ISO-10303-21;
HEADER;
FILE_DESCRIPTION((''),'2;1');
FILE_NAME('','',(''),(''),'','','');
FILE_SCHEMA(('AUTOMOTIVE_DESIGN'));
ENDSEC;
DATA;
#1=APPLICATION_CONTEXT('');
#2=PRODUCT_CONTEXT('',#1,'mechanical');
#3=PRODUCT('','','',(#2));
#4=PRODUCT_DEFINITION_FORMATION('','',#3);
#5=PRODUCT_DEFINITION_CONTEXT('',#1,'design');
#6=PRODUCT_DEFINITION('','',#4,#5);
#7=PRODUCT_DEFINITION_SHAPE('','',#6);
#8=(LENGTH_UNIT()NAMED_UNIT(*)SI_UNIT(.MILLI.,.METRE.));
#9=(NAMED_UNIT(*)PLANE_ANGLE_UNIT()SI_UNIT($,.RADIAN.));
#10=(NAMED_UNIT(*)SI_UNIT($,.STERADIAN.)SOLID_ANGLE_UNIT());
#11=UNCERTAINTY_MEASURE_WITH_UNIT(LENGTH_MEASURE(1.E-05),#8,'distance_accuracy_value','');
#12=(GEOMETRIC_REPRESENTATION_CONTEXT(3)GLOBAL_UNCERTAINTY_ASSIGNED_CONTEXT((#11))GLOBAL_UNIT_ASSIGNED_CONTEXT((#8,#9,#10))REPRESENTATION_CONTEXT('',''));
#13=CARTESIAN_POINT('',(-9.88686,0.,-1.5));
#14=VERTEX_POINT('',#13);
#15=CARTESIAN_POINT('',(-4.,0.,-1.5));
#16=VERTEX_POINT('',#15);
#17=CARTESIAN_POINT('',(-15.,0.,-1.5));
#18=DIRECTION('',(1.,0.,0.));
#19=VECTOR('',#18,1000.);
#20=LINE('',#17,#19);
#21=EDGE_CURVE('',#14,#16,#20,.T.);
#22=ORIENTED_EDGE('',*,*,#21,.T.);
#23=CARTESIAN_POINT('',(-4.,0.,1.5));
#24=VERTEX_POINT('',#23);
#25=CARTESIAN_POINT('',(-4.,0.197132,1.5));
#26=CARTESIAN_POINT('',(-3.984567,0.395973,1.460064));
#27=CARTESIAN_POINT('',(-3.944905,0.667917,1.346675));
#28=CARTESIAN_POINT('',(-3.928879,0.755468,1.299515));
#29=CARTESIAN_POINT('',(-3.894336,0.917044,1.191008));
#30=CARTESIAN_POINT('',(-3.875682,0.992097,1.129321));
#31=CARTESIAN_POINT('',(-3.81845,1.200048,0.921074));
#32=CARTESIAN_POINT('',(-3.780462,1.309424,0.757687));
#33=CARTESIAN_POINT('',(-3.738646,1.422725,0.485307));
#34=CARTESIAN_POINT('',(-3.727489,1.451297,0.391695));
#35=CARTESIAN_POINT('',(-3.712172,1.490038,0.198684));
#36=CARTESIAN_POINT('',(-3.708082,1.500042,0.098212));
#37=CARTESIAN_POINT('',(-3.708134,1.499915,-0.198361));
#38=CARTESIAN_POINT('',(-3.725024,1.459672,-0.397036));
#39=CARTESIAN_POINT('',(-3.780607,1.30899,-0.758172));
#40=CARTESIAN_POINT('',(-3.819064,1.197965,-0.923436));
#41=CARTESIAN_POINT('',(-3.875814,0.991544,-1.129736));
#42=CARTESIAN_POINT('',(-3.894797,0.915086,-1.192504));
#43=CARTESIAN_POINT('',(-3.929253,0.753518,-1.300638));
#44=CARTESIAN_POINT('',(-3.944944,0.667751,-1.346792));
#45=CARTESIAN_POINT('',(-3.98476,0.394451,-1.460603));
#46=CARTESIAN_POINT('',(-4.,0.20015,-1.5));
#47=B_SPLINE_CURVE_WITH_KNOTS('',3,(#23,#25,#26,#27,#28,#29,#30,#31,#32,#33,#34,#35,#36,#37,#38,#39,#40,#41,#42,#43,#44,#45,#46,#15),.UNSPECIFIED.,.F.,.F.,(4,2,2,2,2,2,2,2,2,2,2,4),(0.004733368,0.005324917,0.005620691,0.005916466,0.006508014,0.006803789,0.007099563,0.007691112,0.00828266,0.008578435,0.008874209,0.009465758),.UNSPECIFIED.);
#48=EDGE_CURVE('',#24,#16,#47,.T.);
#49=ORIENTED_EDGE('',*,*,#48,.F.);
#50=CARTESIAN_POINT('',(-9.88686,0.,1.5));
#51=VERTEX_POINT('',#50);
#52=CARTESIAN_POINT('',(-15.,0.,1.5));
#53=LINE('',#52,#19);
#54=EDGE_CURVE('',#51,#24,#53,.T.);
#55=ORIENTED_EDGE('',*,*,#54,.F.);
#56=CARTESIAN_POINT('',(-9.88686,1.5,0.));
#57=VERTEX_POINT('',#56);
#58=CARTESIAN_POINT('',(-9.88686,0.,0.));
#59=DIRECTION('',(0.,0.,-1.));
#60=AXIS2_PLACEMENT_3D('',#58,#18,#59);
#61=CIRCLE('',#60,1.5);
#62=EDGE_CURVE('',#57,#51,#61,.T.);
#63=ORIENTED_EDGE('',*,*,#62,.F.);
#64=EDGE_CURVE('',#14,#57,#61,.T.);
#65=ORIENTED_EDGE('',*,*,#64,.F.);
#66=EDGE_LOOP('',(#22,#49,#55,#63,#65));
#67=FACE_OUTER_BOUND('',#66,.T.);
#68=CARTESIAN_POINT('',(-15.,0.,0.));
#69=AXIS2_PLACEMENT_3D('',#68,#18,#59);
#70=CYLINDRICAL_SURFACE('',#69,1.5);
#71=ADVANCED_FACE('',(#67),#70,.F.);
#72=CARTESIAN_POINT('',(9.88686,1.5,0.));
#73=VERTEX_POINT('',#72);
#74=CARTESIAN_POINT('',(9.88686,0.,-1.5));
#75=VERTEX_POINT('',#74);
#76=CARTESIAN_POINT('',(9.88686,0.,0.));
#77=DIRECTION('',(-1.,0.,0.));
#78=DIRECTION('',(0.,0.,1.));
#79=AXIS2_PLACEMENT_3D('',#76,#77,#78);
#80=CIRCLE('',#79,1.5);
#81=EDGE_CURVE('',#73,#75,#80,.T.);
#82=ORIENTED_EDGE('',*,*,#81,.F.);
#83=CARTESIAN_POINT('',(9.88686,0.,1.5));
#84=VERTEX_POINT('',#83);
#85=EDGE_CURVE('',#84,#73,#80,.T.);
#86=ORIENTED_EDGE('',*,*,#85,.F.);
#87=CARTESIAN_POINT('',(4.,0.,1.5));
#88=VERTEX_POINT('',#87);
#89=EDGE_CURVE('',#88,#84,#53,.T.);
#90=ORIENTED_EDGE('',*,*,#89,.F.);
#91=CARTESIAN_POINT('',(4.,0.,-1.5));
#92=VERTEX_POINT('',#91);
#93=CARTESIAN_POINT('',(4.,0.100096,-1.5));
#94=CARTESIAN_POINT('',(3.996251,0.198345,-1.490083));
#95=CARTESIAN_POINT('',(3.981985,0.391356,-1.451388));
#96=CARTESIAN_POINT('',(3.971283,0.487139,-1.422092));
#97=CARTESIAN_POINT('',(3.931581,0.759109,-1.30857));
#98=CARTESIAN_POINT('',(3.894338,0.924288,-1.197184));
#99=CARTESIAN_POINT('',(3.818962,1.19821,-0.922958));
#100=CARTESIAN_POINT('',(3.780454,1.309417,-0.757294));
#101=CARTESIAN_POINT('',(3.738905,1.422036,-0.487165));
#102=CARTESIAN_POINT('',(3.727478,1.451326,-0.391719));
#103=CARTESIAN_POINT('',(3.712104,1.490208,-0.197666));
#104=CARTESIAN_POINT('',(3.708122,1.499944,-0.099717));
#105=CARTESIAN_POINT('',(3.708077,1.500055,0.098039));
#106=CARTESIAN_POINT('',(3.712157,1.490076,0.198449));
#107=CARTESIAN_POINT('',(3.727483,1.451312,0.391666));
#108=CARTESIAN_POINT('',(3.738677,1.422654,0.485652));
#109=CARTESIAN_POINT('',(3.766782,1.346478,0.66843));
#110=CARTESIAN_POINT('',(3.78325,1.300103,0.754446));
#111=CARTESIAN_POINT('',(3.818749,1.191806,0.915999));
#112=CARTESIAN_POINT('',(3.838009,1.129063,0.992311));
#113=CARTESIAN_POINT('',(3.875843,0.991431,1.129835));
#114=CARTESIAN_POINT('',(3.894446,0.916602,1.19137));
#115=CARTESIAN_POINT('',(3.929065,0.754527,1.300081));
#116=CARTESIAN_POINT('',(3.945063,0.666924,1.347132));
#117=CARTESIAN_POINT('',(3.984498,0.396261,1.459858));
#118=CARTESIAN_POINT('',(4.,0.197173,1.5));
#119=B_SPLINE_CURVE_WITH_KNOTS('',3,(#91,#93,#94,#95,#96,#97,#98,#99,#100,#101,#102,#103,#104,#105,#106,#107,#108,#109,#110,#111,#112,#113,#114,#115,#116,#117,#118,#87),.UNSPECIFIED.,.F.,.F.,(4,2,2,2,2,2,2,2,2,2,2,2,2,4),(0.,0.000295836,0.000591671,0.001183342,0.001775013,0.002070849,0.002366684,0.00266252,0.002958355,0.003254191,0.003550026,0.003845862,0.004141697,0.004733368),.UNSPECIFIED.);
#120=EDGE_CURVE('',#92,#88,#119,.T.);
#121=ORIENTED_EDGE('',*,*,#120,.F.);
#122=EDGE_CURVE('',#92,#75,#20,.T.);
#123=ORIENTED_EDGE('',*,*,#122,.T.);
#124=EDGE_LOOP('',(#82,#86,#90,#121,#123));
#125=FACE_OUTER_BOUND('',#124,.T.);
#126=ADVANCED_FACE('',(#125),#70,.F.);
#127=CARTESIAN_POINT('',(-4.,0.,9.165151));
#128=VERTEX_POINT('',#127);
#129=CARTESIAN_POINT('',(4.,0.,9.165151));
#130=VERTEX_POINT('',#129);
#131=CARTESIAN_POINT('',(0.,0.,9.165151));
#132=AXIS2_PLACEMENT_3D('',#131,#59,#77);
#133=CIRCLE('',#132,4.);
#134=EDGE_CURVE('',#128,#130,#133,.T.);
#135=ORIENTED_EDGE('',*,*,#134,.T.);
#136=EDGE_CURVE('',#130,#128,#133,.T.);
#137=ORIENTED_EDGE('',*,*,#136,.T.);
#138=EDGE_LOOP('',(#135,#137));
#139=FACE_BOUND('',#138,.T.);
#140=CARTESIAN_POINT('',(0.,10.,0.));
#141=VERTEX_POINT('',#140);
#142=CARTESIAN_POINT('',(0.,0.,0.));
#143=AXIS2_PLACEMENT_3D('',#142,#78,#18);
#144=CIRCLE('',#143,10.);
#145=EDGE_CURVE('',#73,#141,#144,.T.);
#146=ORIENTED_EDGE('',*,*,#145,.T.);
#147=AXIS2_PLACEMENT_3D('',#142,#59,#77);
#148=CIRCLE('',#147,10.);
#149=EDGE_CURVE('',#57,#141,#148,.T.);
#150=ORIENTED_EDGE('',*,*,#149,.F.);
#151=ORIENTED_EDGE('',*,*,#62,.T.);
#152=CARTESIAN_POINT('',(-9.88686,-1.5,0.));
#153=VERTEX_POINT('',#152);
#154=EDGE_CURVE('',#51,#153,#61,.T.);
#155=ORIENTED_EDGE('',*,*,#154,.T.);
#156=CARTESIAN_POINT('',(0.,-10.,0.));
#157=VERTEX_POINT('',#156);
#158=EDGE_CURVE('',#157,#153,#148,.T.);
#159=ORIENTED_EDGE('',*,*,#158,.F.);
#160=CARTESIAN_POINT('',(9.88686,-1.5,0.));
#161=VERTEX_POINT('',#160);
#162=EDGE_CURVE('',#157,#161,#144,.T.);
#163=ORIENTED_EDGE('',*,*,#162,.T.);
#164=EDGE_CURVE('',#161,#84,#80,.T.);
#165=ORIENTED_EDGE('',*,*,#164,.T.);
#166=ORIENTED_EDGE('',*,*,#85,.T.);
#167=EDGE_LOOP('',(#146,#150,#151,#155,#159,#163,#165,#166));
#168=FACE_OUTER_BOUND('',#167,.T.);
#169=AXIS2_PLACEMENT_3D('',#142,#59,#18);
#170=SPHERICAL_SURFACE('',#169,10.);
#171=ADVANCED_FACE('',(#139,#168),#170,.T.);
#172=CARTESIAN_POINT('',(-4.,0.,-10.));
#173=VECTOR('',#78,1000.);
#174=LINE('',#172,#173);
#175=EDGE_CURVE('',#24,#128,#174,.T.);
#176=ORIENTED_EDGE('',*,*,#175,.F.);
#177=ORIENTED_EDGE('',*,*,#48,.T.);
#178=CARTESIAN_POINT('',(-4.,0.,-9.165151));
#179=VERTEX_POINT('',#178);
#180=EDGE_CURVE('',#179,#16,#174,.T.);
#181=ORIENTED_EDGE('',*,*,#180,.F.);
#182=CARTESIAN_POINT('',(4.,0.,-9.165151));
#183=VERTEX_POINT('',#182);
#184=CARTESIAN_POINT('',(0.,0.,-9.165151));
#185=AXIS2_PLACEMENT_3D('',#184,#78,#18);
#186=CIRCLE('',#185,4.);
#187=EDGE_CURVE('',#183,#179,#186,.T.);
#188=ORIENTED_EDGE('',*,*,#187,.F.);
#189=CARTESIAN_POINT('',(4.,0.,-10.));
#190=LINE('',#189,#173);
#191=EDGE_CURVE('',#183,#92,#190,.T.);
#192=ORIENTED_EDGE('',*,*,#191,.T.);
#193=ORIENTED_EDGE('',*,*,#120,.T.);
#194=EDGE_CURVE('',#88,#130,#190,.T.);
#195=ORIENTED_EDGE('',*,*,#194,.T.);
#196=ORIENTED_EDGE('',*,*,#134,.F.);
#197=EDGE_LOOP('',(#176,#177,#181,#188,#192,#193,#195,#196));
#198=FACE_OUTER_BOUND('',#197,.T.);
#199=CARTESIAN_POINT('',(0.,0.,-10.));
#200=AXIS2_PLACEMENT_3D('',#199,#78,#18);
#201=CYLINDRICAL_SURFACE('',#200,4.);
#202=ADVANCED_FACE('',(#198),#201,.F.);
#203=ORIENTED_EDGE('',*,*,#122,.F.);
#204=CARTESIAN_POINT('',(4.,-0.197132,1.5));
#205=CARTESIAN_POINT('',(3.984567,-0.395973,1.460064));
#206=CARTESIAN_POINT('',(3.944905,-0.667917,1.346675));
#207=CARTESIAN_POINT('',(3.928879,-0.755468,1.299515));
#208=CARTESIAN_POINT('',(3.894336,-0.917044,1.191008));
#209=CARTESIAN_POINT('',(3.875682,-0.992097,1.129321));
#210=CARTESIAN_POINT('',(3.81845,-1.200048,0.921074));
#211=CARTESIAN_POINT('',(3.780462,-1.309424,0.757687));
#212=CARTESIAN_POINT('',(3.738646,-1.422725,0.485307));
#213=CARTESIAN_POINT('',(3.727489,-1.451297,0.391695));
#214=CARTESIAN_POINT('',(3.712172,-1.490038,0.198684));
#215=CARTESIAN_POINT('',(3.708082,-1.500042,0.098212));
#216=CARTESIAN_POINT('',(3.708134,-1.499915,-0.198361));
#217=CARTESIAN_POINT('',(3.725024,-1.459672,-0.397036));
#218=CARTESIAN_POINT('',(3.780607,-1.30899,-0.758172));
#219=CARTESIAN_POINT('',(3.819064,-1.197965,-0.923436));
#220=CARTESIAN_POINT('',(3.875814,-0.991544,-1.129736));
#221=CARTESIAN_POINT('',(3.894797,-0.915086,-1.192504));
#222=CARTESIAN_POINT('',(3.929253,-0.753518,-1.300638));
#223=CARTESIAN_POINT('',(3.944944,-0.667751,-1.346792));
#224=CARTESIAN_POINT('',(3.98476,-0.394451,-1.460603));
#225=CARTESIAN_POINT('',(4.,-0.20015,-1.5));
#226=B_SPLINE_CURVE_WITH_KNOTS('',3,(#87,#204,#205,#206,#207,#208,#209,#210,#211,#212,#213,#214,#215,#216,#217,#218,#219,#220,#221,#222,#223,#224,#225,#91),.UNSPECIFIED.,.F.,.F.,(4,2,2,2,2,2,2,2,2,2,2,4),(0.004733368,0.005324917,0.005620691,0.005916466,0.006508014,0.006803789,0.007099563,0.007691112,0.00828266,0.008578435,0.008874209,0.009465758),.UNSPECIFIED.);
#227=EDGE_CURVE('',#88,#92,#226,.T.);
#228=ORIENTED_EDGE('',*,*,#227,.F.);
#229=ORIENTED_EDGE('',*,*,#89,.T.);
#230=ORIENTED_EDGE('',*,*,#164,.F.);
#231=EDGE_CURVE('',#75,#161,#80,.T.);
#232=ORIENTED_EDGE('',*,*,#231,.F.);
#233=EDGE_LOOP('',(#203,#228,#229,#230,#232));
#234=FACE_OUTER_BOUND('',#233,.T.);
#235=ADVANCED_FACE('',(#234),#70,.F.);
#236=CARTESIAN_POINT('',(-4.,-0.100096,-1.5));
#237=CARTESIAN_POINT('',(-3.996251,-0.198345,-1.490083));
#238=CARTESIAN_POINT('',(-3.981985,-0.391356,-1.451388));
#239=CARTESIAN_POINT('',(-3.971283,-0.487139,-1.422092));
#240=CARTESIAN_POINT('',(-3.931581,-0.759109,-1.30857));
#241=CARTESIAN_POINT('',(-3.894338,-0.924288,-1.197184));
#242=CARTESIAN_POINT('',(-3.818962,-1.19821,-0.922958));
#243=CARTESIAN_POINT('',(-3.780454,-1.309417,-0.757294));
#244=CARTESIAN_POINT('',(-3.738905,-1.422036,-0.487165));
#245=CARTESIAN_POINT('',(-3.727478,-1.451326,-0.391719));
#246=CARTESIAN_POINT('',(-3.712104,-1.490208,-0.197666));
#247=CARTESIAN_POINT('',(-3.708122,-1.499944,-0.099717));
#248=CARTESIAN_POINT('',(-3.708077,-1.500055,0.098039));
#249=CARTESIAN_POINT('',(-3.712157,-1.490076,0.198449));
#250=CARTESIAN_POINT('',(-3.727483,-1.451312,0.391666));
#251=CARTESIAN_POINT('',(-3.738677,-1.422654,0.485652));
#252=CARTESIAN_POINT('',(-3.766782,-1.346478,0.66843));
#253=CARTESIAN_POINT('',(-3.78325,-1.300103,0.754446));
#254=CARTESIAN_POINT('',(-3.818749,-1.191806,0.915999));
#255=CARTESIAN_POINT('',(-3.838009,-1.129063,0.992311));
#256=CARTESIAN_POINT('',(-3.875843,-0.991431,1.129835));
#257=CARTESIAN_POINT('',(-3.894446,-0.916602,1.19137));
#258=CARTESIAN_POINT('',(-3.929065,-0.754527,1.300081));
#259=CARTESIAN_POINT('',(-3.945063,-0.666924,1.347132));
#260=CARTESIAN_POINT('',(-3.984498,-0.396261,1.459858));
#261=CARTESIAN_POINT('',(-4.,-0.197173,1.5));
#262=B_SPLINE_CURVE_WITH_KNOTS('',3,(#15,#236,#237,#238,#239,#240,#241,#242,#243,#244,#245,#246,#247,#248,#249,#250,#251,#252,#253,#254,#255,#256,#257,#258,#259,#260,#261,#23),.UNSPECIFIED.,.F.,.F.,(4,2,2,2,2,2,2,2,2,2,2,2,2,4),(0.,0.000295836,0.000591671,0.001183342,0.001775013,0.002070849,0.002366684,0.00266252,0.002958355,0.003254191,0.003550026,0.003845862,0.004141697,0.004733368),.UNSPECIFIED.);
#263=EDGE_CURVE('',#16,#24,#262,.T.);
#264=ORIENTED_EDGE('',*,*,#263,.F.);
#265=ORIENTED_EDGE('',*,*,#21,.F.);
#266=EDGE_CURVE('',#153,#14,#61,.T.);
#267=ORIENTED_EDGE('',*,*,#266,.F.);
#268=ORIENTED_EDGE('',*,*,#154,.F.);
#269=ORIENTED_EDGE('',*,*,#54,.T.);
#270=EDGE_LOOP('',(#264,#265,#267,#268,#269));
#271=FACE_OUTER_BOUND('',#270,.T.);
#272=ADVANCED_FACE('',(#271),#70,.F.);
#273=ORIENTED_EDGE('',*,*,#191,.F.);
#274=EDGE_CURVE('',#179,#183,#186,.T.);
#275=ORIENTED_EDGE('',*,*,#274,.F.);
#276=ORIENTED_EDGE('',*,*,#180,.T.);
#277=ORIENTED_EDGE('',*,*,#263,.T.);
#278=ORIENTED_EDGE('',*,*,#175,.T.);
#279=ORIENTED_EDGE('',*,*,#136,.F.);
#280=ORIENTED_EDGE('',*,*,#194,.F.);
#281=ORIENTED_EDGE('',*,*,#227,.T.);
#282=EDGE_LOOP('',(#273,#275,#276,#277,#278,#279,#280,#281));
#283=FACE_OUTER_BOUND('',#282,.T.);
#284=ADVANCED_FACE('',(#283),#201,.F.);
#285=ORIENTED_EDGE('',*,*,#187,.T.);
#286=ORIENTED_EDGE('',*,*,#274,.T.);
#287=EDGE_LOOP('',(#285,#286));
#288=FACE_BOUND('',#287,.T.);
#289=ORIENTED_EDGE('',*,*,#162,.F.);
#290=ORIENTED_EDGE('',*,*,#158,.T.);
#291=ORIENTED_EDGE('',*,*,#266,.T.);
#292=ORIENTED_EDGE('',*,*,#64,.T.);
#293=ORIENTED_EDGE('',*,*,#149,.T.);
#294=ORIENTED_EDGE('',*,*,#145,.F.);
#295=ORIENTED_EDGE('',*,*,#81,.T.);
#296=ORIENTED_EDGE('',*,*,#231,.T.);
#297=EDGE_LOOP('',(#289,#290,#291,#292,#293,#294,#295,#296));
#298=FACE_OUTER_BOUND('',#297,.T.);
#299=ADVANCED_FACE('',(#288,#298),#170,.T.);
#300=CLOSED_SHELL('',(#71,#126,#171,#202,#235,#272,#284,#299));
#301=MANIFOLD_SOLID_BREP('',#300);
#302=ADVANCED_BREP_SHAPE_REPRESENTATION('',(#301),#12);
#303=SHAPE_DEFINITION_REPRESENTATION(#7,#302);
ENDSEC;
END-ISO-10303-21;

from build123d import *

# Parameters (mm, degrees)
SKETCH2_R          = 4
CUT_EXTRUDE1_DEPTH = 10
SKETCH3_R          = 1.5
CUT_EXTRUDE2_DEPTH = 15


with BuildPart() as part:
    # Sketch1 → Revolve1 (revolve)
    with BuildSketch(Plane.XY):
        with BuildLine():
            Line((0, 10), (0, -10))
            ThreePointArc((0, -10), (10, 0), (0, 10))
        make_face()
    revolve(axis=Axis((0, 10, 0), (0, -1, 0)))

    # Sketch2 → Cut-Extrude1 (cut, symmetric)
    with BuildSketch(Plane.XY):
        with Locations(Location((0, 0, 0), (0, 0, 180))):
            Circle(SKETCH2_R)
    extrude(amount=CUT_EXTRUDE1_DEPTH, both=True, mode=Mode.SUBTRACT)

    # Sketch3 → Cut-Extrude2 (cut, symmetric)
    with BuildSketch(Plane(origin=(0, 0, 0), x_dir=(0, 0, -1), z_dir=(1, 0, 0))):
        Circle(SKETCH3_R)
    extrude(amount=CUT_EXTRUDE2_DEPTH, both=True, mode=Mode.SUBTRACT)


solid = part.part
